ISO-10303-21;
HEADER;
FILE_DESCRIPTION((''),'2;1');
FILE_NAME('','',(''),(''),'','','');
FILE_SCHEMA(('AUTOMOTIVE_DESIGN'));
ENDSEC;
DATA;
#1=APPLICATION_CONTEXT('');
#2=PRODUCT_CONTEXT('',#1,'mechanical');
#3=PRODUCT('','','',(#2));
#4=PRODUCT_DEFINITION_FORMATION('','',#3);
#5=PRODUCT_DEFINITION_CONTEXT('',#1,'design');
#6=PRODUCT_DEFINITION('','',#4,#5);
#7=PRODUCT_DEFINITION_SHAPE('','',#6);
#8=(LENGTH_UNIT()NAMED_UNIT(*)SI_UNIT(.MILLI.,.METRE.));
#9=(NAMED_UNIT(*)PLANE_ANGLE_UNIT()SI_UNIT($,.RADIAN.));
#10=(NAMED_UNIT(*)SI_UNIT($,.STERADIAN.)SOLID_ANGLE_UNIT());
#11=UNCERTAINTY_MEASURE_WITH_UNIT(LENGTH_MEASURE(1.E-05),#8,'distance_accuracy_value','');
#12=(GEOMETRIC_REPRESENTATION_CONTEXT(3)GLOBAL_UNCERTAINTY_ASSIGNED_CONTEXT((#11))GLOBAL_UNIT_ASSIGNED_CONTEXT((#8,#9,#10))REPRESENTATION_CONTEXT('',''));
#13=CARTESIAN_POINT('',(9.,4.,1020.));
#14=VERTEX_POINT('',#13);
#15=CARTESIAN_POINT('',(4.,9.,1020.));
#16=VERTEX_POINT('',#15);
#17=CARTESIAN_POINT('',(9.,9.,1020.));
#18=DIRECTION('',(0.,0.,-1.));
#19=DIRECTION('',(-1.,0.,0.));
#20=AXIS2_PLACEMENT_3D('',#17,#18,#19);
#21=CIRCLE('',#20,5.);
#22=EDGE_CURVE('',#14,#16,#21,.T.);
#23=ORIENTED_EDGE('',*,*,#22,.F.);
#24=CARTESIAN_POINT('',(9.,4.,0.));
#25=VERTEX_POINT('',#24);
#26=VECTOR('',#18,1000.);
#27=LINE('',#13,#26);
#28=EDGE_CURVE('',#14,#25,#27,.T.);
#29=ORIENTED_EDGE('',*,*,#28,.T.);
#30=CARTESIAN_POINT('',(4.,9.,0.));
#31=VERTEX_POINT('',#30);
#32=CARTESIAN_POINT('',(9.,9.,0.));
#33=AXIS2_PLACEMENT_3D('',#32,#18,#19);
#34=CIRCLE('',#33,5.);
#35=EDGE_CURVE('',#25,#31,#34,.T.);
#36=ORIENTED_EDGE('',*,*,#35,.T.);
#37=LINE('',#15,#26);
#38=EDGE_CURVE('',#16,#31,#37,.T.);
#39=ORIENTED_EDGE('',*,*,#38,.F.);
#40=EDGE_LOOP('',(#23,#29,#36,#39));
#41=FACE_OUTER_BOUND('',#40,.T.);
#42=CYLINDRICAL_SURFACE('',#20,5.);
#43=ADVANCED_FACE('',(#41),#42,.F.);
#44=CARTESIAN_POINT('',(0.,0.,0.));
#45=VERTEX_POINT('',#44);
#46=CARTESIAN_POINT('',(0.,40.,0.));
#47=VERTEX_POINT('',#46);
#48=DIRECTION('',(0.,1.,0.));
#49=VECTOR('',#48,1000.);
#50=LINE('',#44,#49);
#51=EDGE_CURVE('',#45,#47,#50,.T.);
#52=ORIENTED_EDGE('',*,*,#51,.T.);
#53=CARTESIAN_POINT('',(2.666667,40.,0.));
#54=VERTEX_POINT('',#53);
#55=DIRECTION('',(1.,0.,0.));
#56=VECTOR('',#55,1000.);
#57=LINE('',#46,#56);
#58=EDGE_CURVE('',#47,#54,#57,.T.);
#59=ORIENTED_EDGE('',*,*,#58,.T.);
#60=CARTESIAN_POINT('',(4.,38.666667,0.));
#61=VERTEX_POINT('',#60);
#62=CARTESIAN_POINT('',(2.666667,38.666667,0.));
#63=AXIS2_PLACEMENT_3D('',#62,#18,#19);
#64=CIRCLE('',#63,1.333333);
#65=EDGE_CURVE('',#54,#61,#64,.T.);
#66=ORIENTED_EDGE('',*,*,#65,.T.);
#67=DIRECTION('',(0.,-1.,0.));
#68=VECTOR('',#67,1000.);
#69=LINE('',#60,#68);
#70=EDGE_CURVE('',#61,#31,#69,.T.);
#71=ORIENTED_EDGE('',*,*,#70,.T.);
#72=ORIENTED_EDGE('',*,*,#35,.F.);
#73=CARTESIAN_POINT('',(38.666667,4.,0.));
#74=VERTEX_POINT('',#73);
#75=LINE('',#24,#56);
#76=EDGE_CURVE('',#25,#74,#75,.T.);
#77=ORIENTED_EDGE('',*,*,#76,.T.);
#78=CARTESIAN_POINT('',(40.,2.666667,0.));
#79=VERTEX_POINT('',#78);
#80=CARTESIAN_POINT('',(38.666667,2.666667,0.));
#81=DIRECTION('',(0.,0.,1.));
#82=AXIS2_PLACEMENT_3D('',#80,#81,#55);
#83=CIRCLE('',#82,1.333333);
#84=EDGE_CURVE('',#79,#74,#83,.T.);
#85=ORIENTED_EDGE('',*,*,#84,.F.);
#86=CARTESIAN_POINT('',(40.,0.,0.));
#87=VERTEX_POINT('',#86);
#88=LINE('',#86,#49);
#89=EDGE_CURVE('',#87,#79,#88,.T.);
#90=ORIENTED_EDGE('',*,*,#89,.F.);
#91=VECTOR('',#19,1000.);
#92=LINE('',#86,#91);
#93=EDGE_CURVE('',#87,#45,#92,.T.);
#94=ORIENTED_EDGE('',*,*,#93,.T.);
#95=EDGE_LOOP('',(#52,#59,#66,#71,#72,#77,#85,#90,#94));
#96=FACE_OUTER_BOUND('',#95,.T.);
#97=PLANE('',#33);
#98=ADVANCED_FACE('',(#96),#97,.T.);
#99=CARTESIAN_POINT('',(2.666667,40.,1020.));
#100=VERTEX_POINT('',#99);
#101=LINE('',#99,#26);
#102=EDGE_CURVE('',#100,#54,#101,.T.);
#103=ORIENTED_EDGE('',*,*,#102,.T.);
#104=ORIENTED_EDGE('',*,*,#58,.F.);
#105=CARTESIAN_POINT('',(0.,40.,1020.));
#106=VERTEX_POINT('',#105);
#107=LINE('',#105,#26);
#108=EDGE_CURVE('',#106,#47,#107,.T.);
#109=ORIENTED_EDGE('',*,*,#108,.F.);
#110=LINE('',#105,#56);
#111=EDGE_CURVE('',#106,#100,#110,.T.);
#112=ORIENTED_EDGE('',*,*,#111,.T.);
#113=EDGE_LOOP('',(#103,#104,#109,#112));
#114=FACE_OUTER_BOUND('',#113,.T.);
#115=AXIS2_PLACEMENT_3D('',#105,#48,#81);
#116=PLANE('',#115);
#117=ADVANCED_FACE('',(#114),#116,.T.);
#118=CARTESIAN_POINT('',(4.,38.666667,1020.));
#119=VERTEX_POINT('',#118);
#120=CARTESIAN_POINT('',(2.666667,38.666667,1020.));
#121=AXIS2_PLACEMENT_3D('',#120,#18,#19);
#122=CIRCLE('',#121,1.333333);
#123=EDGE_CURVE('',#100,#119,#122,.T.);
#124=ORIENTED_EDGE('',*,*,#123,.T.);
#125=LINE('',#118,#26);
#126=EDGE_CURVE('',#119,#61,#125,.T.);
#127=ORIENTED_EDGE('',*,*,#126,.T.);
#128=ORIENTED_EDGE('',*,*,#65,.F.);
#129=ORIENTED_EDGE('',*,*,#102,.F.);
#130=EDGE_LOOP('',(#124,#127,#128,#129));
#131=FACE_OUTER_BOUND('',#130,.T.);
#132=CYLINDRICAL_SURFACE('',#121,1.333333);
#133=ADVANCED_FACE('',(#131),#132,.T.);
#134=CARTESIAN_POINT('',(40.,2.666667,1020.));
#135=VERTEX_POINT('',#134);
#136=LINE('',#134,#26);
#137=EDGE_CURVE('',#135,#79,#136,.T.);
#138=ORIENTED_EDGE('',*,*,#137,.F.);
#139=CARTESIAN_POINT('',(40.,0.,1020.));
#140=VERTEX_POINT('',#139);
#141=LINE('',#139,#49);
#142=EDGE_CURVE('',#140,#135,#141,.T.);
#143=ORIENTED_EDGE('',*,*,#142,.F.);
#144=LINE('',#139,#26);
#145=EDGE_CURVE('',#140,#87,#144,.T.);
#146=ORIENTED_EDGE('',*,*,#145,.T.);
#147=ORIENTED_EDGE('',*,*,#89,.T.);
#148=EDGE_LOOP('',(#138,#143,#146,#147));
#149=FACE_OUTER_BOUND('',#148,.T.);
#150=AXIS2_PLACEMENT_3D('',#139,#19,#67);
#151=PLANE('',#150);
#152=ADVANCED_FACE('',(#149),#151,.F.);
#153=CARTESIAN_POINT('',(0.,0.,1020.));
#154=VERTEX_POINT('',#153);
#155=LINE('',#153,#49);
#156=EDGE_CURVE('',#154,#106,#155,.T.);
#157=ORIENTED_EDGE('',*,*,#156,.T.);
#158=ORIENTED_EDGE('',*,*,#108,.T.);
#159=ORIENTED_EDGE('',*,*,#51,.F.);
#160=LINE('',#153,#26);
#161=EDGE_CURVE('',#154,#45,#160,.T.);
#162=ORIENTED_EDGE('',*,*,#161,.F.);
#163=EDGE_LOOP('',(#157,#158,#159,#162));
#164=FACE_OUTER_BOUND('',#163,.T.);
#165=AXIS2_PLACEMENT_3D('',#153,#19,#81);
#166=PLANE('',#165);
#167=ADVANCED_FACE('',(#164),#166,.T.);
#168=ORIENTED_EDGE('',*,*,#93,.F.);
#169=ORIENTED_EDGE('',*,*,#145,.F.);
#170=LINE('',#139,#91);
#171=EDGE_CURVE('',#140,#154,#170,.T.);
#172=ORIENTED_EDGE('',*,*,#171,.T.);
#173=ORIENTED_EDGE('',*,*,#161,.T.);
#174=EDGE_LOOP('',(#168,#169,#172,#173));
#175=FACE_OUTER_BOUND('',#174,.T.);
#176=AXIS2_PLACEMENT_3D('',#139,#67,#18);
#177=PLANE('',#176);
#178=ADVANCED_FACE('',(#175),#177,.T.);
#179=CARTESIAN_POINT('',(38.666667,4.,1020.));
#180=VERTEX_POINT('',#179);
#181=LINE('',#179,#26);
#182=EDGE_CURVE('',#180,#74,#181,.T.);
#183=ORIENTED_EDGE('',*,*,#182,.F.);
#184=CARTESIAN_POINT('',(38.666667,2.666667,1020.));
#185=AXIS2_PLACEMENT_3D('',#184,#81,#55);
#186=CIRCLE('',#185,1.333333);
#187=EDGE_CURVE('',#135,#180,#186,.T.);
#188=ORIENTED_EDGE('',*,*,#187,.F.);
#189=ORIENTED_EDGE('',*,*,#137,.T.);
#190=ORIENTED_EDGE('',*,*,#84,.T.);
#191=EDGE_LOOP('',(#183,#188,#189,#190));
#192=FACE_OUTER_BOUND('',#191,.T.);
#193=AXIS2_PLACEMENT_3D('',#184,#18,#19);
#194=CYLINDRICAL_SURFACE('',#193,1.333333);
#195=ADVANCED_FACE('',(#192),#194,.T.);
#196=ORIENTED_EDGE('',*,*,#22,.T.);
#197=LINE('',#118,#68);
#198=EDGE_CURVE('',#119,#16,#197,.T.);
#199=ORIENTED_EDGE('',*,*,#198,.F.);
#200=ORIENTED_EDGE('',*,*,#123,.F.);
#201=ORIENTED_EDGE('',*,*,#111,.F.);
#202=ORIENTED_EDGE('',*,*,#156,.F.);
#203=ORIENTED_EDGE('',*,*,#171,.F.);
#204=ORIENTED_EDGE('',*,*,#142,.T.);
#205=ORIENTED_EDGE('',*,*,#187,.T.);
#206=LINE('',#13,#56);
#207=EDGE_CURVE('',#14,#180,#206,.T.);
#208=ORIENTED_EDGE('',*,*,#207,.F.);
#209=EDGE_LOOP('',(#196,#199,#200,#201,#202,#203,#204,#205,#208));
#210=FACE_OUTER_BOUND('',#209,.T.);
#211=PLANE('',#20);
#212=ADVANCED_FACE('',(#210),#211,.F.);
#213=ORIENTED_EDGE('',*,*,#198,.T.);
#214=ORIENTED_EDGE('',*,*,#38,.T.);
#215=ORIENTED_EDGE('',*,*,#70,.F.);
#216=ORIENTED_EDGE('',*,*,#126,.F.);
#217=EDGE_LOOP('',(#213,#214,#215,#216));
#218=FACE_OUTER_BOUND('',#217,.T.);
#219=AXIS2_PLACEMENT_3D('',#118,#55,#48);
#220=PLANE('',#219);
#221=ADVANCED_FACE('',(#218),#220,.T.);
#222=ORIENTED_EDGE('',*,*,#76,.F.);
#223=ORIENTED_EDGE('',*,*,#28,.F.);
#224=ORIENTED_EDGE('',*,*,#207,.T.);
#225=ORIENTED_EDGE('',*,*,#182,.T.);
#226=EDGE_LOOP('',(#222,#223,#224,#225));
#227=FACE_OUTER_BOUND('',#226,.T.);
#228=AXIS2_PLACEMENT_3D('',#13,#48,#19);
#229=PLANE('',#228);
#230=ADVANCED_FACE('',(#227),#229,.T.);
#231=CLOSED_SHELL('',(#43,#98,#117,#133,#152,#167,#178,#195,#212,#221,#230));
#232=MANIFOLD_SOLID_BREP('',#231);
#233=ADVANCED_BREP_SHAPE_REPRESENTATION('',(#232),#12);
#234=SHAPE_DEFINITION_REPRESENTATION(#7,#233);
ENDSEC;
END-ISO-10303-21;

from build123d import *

# Parameters (mm, degrees)
BOSS_EXTRUDE1_DEPTH = 1020


with BuildPart() as part:
    # Sketch1 → Boss-Extrude1 (new body)
    with BuildSketch(Plane.XY):
        with BuildLine():
            Line((0, 0), (0, 40))
            Line((0, 40), (2.666666667, 40))
            ThreePointArc((2.666666667, 40), (3.609475708, 39.609475708), (4, 38.666666667))
            Line((4, 38.666666667), (4, 9))
            ThreePointArc((4, 9), (5.464466094, 5.464466094), (9, 4))
            Line((9, 4), (38.666666667, 4))
            ThreePointArc((38.666666667, 4), (39.609475708, 3.609475708), (40, 2.666666667))
            Line((40, 2.666666667), (40, 0))
            Line((40, 0), (0, 0))
        make_face()
    extrude(amount=BOSS_EXTRUDE1_DEPTH)


solid = part.part
